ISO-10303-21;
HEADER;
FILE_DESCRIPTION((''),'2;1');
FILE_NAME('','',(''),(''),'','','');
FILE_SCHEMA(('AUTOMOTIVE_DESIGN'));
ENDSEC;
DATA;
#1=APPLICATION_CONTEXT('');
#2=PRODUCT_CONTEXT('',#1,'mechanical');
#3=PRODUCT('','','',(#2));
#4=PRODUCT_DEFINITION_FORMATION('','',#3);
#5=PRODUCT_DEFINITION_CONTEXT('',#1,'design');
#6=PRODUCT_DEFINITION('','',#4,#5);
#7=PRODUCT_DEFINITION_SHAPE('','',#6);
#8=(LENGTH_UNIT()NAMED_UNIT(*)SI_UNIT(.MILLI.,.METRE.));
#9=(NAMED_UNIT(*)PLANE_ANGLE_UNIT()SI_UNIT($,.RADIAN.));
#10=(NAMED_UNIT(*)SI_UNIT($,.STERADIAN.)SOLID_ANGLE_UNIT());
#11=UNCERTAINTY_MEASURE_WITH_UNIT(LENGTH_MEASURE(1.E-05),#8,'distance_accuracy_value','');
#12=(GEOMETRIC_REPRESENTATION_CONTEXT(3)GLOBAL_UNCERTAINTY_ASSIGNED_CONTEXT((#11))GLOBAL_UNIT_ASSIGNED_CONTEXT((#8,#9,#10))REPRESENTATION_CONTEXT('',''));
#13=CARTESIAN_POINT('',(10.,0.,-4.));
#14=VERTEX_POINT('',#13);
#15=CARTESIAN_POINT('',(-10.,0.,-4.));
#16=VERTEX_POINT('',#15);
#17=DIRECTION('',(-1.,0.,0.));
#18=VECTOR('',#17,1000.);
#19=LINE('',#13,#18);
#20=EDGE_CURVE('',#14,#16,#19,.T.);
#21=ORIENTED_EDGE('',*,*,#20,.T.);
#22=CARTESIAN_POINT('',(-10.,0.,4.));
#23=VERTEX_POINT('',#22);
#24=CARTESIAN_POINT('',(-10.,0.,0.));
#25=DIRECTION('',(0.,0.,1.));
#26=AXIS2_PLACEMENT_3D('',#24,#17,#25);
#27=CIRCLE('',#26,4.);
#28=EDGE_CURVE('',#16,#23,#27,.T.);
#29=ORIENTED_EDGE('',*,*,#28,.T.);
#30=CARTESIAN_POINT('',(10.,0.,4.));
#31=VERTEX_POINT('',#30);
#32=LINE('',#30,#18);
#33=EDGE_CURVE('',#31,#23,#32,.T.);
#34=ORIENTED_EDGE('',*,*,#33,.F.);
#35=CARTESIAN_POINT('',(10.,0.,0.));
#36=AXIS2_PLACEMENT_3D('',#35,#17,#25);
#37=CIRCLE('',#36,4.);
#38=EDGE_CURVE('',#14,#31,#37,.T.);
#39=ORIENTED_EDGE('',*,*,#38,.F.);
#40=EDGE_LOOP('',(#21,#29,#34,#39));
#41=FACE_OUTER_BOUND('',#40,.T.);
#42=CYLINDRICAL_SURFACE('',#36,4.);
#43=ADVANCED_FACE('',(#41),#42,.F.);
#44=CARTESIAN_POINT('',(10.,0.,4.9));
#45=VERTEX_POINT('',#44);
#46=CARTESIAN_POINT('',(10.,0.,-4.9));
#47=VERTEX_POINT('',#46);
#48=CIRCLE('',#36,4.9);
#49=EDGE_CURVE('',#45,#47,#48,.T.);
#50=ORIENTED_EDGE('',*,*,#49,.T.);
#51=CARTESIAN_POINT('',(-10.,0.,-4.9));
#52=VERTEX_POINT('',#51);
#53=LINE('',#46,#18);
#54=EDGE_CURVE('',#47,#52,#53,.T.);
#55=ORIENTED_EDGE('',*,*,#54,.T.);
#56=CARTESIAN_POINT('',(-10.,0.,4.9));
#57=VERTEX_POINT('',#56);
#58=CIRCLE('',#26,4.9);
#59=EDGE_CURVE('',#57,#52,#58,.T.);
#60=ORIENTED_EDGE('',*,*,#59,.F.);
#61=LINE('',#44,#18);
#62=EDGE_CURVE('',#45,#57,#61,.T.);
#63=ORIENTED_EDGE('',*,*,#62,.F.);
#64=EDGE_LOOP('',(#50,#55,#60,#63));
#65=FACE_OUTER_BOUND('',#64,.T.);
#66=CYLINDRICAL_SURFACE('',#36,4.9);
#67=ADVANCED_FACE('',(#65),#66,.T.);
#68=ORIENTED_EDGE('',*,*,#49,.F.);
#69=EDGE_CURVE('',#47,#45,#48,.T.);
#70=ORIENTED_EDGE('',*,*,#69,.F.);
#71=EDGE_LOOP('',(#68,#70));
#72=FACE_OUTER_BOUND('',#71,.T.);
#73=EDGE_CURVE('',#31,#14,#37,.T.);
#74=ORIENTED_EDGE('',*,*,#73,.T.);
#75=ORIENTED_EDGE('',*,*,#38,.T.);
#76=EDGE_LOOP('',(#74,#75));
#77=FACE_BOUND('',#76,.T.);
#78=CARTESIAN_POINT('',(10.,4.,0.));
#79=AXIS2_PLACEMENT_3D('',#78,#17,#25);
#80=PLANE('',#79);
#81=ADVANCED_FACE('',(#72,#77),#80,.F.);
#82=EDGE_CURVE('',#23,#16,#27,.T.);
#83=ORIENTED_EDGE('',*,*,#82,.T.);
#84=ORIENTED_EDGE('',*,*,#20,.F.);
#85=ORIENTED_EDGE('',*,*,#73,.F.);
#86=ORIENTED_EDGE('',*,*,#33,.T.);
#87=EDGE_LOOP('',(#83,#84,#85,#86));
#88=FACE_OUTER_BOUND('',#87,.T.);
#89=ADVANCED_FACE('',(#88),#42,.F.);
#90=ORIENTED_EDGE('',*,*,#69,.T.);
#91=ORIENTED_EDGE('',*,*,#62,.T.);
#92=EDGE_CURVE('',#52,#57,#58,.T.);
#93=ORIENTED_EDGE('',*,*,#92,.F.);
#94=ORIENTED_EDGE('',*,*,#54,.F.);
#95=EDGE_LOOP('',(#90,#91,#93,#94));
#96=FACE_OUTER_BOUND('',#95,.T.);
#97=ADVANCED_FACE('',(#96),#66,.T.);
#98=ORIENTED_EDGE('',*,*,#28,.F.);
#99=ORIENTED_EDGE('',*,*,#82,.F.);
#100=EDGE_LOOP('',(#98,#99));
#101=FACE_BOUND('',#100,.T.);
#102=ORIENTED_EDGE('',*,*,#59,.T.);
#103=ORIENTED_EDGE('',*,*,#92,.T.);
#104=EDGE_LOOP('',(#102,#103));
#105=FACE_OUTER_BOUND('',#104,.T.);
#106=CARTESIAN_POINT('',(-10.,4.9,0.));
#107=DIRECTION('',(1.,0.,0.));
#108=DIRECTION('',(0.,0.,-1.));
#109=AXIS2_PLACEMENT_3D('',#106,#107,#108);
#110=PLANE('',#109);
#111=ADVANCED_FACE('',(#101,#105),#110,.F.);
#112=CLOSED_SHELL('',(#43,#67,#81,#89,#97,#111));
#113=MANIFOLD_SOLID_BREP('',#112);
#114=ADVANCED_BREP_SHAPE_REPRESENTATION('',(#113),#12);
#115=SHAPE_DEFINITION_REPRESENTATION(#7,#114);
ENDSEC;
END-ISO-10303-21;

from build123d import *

# Parameters (mm, degrees)
SKETCH1_W = 20
SKETCH1_H = 0.9


with BuildPart() as part:
    # Sketch1 → Revolve1 (revolve)
    with BuildSketch(Plane.XY, mode=Mode.PRIVATE) as revolve1_sk:
        with Locations((0, 4.45)):
            Rectangle(SKETCH1_W, SKETCH1_H)
    revolve(revolve1_sk.sketch.rotate(Axis((10, 0, 0), (-1, 0, 0)), 270), axis=Axis((10, 0, 0), (-1, 0, 0)))


solid = part.part
